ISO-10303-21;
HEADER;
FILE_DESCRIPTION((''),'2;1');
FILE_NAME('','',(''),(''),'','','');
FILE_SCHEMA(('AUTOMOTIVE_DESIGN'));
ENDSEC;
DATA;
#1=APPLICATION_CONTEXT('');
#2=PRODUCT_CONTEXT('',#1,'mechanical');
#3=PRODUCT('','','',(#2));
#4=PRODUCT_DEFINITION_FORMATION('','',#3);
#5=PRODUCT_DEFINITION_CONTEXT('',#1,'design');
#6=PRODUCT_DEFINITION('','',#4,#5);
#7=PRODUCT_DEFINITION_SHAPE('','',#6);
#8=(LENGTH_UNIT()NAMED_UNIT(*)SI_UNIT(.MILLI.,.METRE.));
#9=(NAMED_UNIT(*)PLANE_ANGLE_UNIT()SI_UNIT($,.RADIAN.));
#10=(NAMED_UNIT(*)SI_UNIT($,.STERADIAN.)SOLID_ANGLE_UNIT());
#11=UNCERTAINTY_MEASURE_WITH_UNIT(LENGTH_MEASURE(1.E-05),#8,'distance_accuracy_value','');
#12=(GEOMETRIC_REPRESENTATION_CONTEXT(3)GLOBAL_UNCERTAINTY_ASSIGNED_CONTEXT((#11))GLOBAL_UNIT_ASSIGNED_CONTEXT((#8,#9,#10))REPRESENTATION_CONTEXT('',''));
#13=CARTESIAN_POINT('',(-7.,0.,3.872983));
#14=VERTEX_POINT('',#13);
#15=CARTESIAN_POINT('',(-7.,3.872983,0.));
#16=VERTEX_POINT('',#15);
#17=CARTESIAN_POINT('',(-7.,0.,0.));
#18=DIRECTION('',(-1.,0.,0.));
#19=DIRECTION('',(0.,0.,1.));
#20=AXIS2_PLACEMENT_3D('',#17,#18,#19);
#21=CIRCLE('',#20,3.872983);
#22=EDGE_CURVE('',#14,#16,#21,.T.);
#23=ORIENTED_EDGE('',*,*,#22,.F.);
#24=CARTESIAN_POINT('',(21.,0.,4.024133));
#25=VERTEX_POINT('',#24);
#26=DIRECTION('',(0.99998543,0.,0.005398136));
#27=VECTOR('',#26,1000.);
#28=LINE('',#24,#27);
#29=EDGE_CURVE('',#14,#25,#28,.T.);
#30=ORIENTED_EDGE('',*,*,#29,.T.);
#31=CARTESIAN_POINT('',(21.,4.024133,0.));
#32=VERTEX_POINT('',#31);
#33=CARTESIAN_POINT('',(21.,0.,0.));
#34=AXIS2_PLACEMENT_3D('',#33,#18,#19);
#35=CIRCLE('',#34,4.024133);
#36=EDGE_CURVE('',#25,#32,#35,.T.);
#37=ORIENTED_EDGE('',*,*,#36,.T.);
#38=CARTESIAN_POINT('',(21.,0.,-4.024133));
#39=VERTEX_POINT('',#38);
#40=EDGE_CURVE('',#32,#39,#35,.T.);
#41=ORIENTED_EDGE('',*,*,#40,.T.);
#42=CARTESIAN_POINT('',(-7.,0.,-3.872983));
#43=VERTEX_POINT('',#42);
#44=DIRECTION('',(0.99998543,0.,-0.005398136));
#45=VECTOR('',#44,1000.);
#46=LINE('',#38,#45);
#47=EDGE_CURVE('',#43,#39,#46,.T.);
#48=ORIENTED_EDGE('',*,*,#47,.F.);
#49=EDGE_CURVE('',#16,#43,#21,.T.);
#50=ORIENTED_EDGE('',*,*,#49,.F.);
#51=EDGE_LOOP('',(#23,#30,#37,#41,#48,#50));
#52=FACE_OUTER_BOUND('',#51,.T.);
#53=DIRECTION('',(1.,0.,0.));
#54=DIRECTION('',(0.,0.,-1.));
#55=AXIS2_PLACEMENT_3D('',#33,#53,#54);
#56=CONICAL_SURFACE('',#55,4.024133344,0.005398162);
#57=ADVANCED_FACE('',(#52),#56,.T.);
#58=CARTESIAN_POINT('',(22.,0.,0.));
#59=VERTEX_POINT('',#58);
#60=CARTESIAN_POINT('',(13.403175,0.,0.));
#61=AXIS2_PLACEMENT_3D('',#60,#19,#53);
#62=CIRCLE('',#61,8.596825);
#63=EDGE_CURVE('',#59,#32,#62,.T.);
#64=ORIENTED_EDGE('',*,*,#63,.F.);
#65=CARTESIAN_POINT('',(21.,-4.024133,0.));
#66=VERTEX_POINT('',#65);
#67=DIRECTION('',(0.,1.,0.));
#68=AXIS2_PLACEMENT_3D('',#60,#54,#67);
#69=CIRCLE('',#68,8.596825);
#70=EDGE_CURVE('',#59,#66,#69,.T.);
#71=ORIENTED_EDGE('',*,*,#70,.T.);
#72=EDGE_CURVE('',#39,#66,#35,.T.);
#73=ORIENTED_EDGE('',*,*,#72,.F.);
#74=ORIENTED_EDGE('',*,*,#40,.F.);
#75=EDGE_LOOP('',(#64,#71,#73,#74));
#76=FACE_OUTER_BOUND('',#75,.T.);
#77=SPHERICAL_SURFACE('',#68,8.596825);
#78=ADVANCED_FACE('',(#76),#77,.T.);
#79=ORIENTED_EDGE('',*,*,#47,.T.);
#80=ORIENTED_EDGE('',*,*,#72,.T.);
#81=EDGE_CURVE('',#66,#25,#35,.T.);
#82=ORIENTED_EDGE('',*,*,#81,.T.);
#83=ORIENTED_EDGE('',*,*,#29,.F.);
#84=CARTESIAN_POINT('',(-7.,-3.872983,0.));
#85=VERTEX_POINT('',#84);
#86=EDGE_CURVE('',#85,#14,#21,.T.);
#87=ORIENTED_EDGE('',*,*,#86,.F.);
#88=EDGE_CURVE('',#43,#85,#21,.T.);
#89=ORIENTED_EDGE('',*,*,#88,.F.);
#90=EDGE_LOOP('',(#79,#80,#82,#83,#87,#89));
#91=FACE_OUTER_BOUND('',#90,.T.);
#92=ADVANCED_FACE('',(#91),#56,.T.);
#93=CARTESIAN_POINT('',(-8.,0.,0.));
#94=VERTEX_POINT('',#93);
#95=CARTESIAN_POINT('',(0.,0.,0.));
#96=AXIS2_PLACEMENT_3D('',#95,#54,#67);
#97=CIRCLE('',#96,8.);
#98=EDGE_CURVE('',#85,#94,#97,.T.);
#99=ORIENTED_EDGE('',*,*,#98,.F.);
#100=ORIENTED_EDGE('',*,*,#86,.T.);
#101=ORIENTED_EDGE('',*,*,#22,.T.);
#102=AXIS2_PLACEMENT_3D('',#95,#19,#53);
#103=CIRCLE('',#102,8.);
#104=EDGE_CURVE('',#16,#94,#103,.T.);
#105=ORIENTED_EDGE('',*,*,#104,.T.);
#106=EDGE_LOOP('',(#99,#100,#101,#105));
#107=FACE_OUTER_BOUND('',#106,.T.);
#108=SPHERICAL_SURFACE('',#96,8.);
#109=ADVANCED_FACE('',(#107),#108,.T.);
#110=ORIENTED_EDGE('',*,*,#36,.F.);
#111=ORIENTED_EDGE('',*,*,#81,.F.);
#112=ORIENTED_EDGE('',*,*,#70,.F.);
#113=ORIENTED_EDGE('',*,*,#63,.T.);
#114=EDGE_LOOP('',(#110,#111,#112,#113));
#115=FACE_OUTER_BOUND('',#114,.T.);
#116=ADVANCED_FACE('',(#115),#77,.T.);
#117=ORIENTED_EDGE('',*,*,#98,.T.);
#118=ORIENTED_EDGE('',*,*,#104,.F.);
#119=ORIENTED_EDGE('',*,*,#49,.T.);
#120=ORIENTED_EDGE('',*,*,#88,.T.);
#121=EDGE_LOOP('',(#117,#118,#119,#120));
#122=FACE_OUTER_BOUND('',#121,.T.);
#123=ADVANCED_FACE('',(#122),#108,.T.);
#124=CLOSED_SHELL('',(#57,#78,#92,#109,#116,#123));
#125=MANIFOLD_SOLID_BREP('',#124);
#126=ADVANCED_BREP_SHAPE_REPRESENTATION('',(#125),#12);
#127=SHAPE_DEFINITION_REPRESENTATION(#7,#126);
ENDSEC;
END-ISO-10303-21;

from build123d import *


with BuildPart() as part:
    # Sketch1 → Revolve1 (revolve)
    with BuildSketch(Plane.XY):
        with BuildLine():
            Line((-7, 3.872983346), (21, 4.024133344))
            ThreePointArc((21, 4.024133344), (21.746255221, 2.07326127), (22, 0))
            Line((22, 0), (-8, 0))
            ThreePointArc((-8, 0), (-7.745966692, 2), (-7, 3.872983346))
        make_face()
    revolve(axis=Axis((-8, 0, 0), (1, 0, 0)))


solid = part.part
